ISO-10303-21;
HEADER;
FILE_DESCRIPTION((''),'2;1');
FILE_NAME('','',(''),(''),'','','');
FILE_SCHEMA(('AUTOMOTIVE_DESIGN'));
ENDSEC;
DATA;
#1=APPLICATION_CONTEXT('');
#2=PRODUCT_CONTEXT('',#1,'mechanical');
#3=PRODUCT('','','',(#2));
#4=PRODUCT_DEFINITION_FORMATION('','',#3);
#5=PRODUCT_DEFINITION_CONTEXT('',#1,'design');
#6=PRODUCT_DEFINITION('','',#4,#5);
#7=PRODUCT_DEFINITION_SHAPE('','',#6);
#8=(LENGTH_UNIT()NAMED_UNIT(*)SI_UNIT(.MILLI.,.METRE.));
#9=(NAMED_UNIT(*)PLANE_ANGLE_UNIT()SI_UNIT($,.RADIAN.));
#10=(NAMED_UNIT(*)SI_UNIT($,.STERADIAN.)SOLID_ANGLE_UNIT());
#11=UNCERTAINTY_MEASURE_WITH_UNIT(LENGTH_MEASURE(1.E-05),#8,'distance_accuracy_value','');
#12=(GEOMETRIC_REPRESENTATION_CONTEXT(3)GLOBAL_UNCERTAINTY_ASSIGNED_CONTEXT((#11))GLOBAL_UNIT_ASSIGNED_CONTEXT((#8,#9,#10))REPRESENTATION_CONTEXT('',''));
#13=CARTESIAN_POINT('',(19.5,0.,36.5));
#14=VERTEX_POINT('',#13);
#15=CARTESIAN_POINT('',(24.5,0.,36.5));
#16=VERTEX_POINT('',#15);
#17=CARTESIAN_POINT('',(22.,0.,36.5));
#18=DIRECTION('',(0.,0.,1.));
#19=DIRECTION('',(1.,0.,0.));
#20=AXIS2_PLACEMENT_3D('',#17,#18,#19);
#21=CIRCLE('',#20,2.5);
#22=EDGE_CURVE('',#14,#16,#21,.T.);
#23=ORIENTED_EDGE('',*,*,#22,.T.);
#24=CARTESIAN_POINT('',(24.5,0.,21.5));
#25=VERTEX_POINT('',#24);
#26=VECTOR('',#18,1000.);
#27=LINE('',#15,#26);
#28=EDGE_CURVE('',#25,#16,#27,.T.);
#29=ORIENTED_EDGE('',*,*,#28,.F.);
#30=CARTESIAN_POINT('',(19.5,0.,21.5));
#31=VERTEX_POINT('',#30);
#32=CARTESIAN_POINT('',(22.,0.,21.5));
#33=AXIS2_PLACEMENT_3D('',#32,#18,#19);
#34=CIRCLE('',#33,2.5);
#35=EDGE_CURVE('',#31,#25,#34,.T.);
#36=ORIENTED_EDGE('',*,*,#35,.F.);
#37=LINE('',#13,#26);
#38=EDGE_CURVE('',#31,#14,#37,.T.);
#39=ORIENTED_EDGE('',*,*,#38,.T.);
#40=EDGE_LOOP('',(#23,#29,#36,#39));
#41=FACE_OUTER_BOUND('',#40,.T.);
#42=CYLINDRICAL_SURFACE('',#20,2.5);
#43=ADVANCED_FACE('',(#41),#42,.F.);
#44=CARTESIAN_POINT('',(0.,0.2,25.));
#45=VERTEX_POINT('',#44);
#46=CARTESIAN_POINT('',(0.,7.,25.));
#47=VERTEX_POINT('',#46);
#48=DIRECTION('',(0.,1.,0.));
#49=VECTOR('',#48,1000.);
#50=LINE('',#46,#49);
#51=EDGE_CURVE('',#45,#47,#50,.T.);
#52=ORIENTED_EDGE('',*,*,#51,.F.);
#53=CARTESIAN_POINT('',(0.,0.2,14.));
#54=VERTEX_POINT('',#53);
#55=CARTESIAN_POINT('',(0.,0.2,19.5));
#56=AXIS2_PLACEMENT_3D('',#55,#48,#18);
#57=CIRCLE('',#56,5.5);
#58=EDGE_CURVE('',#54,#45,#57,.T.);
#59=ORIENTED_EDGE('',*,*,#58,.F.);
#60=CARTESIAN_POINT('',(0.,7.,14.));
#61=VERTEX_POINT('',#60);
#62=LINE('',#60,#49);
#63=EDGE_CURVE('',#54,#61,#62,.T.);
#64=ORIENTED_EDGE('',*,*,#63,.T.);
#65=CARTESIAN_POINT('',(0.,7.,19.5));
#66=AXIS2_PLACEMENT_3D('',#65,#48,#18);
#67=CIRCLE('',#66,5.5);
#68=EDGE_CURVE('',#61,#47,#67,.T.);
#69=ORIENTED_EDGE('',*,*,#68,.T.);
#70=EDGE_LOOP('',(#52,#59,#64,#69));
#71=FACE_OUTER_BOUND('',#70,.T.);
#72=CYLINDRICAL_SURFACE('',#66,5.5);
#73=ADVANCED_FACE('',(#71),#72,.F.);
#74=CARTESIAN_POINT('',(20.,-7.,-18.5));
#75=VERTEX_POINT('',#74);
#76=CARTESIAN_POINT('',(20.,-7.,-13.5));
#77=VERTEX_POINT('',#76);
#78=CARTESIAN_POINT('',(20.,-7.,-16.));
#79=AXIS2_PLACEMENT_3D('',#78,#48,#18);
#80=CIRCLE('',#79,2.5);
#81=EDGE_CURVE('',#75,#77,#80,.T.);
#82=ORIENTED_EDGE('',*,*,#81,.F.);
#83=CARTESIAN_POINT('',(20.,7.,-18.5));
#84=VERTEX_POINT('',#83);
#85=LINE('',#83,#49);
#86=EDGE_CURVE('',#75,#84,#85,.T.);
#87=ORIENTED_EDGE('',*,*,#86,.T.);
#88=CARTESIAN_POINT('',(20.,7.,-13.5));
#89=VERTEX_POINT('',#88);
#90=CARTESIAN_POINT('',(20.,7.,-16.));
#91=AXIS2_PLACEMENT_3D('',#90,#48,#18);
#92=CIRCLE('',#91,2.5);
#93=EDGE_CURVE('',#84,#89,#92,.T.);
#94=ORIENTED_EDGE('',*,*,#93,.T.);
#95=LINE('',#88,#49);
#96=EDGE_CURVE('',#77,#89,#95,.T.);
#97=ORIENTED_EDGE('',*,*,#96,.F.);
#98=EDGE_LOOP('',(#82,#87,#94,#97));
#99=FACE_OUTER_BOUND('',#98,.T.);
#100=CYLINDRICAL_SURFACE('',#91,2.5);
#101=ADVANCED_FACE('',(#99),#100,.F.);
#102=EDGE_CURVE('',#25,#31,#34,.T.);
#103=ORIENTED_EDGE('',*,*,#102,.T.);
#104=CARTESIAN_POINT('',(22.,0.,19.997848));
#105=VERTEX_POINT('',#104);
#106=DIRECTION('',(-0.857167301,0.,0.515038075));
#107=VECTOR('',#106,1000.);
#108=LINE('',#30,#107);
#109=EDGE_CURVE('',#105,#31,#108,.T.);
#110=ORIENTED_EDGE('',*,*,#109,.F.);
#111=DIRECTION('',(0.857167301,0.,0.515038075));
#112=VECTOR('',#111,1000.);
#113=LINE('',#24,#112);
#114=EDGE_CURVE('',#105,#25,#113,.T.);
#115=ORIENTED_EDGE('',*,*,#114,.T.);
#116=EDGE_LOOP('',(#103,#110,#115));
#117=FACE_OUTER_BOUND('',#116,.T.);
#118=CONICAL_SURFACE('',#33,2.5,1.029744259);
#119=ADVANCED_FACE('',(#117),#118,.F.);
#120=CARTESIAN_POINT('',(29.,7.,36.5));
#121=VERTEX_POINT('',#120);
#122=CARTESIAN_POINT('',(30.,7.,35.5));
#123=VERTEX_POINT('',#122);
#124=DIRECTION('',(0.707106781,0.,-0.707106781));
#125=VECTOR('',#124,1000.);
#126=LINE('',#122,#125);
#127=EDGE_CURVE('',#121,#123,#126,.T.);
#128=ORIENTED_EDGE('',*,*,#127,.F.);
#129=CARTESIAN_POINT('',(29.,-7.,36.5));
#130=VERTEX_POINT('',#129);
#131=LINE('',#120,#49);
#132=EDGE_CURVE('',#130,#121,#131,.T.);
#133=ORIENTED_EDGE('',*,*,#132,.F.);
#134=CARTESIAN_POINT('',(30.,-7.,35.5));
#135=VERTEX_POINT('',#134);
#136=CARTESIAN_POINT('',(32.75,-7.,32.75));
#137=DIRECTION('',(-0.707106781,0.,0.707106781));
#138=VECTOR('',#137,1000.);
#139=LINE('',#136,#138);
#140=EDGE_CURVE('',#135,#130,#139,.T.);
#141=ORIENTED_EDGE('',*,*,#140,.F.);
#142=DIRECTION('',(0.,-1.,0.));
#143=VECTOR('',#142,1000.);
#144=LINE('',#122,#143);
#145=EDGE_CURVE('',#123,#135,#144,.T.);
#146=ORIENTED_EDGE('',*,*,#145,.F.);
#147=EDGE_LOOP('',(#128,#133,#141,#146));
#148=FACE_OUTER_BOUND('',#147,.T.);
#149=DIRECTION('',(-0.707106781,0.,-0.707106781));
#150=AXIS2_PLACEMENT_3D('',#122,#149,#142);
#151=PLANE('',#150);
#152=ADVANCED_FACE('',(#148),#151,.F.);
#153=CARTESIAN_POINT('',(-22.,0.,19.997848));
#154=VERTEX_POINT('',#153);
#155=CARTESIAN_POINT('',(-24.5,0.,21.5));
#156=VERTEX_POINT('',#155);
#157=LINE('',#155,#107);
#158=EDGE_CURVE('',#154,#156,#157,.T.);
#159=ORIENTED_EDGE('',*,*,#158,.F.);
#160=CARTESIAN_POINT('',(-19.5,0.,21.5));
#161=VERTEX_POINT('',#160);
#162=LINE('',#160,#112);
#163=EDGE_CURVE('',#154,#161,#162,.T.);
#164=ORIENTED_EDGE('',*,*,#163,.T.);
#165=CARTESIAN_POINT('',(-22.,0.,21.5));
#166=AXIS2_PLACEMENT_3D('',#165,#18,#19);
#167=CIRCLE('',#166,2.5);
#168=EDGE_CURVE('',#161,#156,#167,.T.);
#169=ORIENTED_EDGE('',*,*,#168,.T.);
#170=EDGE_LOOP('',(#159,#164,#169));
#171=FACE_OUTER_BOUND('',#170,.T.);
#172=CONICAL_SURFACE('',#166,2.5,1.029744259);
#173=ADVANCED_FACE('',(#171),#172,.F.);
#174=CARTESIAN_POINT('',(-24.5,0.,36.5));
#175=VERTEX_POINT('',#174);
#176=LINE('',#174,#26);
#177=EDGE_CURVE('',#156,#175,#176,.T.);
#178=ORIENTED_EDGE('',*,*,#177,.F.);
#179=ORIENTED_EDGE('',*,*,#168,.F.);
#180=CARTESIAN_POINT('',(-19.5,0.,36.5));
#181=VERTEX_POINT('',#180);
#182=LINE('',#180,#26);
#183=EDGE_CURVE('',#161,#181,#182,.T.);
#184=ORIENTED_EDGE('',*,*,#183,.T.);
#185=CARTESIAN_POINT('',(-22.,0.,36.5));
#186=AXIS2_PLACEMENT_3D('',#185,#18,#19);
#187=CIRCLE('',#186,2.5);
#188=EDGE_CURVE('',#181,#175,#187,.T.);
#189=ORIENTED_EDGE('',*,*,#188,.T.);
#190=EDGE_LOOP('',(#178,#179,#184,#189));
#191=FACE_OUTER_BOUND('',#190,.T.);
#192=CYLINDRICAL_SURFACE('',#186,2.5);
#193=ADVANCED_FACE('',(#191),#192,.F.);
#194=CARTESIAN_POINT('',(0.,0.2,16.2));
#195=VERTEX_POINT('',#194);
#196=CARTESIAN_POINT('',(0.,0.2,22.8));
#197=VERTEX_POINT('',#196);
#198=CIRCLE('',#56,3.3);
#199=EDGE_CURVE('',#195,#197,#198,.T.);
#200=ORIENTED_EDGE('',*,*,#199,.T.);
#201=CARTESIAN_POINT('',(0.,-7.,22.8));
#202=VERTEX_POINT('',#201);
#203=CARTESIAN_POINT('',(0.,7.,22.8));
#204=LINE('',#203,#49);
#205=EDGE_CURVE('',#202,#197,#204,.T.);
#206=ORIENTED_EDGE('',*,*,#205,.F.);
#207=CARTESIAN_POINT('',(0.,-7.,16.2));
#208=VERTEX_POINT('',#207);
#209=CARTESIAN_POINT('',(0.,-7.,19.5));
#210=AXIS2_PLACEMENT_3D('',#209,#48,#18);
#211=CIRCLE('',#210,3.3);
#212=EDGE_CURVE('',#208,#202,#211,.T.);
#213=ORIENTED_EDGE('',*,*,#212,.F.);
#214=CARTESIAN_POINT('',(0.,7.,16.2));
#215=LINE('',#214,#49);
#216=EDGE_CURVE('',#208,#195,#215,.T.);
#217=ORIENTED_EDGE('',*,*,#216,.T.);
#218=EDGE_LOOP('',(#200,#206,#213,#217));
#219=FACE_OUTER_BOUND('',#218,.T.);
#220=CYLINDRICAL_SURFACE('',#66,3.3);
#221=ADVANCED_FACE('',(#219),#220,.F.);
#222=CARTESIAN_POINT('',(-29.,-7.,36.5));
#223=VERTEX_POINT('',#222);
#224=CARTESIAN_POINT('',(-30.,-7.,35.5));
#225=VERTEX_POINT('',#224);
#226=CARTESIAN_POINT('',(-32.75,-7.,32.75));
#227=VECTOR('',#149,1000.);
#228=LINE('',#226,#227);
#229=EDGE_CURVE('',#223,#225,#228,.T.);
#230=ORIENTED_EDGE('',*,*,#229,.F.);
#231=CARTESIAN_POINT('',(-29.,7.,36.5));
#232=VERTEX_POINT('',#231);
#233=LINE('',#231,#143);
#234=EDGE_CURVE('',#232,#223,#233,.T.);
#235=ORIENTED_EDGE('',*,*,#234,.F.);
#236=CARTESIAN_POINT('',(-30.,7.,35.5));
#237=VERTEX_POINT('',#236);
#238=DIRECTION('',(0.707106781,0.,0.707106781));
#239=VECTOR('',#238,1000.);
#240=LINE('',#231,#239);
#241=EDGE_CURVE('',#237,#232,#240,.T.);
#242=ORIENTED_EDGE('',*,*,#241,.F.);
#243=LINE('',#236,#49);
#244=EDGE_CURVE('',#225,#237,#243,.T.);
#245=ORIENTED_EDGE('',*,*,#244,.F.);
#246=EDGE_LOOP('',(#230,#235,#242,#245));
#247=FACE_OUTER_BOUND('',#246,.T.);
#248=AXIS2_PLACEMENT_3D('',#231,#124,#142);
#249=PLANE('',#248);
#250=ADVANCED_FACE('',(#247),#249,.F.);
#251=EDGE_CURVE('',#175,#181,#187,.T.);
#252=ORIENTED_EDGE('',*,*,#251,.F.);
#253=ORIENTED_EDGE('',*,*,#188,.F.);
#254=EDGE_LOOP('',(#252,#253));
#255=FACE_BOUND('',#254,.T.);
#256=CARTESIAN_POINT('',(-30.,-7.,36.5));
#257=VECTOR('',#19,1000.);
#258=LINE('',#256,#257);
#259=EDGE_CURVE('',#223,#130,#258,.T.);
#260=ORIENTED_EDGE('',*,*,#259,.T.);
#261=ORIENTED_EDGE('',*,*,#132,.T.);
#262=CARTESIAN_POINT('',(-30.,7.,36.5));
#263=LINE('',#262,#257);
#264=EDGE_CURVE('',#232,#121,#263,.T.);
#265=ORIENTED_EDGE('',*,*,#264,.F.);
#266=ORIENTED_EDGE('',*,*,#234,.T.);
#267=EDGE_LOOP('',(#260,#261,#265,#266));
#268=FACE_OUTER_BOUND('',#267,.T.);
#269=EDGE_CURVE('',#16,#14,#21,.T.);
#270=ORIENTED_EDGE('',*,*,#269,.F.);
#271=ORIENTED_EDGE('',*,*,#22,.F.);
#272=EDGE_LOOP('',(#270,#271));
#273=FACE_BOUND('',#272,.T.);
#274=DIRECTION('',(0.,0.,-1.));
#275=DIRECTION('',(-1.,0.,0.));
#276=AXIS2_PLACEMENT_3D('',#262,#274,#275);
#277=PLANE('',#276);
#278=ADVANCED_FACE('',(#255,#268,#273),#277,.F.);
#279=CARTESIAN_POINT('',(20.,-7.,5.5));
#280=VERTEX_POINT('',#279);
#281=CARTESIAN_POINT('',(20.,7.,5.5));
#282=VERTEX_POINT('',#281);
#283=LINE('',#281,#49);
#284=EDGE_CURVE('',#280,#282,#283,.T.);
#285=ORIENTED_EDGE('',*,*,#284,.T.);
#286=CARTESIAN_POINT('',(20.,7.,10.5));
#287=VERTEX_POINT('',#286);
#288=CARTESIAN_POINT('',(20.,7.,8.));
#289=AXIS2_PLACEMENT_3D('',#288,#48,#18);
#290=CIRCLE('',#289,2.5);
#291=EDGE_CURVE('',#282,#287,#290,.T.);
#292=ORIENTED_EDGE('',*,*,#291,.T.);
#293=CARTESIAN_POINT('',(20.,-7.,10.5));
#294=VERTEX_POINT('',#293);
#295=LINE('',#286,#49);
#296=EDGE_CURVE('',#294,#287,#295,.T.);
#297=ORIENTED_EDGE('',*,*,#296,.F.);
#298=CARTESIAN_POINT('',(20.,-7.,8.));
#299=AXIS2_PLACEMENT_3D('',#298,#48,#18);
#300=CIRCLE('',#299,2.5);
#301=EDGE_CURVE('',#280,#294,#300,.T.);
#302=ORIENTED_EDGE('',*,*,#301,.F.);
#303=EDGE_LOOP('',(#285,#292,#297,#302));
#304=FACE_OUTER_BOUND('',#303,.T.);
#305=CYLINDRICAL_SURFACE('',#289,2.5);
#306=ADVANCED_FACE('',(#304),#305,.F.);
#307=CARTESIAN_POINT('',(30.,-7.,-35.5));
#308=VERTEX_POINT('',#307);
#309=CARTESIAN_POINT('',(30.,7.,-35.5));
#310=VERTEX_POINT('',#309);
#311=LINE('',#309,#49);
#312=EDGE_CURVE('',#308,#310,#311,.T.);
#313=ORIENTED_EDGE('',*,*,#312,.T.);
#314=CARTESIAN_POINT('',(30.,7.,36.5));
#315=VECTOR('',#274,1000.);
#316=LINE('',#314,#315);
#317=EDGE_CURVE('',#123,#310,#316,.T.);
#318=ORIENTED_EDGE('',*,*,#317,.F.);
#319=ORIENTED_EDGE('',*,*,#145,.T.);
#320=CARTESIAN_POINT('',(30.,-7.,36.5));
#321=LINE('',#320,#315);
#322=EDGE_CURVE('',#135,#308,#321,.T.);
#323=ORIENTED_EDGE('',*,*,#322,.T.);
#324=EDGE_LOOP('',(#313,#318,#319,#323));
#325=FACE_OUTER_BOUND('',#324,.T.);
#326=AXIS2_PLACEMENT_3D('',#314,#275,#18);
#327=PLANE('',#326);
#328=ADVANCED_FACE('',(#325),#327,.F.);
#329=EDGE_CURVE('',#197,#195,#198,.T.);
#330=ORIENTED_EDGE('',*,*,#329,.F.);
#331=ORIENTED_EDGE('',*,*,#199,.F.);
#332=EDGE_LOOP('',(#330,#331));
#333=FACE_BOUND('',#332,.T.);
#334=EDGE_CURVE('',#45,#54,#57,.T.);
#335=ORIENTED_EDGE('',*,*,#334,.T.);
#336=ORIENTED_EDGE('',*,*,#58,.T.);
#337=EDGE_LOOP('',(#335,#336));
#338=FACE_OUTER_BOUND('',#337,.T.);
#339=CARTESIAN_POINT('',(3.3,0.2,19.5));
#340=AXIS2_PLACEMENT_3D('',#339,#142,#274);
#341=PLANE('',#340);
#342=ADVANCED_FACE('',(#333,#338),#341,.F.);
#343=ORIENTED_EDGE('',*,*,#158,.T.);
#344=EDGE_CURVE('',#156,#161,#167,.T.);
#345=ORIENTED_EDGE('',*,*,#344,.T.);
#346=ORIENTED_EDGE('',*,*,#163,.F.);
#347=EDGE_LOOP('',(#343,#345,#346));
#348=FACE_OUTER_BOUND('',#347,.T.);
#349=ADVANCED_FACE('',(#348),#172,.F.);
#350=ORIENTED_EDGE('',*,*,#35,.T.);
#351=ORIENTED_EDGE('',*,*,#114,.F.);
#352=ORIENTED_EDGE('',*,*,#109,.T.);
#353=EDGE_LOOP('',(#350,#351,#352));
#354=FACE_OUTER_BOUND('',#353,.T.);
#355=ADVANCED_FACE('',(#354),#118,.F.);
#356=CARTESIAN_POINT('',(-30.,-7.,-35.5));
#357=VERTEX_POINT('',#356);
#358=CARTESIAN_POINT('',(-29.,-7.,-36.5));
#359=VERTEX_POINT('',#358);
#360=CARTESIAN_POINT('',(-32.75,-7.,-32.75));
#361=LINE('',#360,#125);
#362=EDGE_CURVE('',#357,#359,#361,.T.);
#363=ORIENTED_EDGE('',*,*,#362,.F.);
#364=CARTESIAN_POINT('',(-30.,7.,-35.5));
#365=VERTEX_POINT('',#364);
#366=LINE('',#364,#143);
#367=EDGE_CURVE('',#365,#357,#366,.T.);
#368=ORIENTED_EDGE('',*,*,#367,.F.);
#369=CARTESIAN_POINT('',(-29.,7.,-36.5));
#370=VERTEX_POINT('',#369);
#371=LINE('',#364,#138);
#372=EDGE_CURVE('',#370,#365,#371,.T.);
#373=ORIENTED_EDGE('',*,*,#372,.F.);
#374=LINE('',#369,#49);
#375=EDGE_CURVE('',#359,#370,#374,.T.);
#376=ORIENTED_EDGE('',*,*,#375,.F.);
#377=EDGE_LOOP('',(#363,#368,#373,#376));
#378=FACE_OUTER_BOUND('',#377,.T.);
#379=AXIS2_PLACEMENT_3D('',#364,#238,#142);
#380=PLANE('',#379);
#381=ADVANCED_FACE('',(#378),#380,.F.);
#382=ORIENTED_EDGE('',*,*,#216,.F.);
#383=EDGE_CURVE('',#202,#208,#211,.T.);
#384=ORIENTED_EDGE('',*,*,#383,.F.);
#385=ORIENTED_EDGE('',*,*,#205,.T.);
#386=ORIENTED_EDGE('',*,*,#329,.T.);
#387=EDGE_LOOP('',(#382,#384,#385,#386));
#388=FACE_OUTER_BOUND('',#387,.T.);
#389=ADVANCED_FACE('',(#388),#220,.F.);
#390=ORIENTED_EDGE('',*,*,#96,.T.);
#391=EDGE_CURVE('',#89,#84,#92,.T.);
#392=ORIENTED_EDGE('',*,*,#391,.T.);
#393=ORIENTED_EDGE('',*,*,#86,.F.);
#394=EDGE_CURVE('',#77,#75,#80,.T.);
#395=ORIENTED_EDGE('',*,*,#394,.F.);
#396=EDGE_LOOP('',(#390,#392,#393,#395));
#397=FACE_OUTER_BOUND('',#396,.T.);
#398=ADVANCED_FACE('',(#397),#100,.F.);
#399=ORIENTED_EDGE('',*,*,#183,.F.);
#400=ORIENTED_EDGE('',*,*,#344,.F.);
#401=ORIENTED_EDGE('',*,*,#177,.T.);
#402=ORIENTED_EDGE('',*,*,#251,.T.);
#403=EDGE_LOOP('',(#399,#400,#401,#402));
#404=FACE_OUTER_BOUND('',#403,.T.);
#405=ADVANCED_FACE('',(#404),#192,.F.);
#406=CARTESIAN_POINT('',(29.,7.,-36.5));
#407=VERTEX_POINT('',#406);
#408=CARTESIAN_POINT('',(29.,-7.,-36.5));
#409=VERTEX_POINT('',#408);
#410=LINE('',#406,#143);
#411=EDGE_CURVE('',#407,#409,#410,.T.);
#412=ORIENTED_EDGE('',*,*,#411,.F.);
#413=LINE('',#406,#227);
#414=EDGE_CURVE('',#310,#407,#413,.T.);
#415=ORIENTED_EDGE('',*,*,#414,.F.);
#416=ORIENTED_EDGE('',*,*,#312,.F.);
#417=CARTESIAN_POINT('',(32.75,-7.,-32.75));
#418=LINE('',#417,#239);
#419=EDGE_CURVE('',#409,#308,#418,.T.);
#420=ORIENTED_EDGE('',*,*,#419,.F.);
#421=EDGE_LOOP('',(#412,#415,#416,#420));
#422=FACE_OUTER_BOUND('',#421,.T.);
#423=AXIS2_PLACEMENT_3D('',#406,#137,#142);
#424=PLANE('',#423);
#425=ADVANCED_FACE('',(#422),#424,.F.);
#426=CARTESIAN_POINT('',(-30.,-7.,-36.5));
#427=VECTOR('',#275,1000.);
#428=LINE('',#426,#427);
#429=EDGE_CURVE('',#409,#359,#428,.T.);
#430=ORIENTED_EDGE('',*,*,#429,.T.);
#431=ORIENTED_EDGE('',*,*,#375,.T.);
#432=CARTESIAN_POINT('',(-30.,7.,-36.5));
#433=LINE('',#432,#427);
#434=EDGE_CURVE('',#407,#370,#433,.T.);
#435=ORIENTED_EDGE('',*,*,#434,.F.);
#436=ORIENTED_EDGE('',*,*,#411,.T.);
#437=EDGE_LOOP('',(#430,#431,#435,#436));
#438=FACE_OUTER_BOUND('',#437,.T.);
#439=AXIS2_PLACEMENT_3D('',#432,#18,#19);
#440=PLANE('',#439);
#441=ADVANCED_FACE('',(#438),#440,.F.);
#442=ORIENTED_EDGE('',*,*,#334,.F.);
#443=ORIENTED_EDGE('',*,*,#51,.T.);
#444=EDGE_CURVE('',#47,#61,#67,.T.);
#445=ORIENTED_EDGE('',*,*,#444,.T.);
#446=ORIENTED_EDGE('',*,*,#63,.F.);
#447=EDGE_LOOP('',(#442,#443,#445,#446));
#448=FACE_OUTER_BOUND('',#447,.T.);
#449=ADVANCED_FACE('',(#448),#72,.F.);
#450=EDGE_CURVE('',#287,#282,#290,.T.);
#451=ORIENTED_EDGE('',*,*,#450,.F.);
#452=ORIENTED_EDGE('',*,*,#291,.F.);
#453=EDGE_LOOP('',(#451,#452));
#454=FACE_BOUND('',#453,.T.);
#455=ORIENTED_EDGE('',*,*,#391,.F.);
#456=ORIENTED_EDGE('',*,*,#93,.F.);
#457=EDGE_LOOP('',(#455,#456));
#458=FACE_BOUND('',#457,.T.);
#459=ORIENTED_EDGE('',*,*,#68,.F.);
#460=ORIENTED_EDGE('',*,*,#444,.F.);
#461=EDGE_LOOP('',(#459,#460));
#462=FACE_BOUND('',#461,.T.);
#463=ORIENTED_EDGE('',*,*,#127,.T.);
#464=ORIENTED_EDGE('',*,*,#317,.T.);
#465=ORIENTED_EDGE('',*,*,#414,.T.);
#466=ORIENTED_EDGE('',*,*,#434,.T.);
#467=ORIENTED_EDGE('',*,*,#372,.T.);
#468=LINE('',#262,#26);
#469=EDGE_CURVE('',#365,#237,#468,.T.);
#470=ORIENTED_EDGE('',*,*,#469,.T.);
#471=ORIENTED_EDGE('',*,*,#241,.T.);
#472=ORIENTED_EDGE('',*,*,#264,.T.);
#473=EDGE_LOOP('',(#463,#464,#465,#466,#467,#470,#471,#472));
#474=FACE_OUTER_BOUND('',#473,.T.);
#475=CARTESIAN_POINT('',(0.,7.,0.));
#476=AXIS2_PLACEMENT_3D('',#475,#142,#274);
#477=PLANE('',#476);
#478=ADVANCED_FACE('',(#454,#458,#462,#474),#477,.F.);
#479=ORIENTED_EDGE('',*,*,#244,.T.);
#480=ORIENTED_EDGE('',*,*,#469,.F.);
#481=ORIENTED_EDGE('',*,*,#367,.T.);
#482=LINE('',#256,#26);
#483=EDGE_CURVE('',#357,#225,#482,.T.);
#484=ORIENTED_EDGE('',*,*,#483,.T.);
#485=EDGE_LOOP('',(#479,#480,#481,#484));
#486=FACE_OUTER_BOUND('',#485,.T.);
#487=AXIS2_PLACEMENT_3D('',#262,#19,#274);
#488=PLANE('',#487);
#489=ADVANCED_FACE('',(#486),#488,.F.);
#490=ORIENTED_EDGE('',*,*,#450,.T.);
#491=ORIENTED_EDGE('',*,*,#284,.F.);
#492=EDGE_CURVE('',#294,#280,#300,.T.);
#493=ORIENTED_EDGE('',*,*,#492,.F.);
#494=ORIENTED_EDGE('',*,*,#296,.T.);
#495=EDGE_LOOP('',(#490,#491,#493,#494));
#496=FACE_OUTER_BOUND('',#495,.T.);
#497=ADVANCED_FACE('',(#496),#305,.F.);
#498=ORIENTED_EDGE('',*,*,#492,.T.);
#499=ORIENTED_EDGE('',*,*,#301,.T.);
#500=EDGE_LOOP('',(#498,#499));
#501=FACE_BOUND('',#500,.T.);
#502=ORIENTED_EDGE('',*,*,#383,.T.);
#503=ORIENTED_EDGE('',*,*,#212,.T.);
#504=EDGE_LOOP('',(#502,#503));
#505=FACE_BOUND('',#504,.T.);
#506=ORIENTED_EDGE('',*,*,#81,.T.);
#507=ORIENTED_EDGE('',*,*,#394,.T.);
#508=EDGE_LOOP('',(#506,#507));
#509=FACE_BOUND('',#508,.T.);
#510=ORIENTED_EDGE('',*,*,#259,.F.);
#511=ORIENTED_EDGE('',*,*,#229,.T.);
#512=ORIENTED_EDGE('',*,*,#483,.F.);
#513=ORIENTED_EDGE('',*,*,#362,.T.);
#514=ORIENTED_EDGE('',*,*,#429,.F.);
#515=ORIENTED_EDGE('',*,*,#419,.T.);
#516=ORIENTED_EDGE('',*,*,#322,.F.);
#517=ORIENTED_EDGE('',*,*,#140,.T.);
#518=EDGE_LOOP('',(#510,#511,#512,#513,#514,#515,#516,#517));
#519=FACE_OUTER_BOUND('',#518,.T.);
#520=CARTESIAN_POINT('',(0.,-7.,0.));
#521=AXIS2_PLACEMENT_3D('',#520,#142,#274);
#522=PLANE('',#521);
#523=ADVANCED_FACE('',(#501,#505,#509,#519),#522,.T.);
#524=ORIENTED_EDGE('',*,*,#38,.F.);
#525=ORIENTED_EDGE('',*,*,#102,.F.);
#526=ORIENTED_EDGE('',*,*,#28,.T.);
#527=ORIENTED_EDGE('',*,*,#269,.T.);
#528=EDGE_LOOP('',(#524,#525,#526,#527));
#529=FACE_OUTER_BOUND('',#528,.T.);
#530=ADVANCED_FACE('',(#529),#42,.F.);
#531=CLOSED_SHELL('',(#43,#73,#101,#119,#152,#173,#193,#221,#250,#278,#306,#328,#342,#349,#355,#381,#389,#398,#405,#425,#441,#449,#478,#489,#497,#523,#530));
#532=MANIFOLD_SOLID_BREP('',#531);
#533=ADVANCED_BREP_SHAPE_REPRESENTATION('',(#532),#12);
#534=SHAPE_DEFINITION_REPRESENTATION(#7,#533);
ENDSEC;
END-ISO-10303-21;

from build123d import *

# Parameters (mm, degrees)
SKETCH1_W                                            = 60
SKETCH1_H                                            = 73
BOSS_EXTRUDE1_DEPTH                                  = 7
M6_TAPPED_HOLE1_D                                    = 5
M6_TAPPED_HOLE1_DEPTH                                = 15
M6_TAPPED_HOLE1_TIP                                  = 1.502151548
M6_TAPPED_HOLE2_D                                    = 5
CHAMFER1_SIZE                                        = 1
HOLE_SIZE_PER_SOCKET_HEAD_CAP_SCREW_TYPE_D           = 6.6
HOLE_SIZE_PER_SOCKET_HEAD_CAP_SCREW_TYPE_CBORE_D     = 11
HOLE_SIZE_PER_SOCKET_HEAD_CAP_SCREW_TYPE_CBORE_DEPTH = 6.8


with BuildPart() as part:
    # Sketch1 → Boss-Extrude1 (new, symmetric)
    with BuildSketch(Plane(origin=(0, 0, 0), x_dir=(1, 0, 0), z_dir=(0, 1, 0))):
        Rectangle(SKETCH1_W, SKETCH1_H)
    extrude(amount=BOSS_EXTRUDE1_DEPTH, both=True)

    # M6 Tapped Hole1
    with Locations(Plane.XY.offset(36.5)):
        with Locations((22, 0), (-22, 0)):
            Hole(M6_TAPPED_HOLE1_D / 2, depth=M6_TAPPED_HOLE1_DEPTH)
            with Locations((0, 0, -(M6_TAPPED_HOLE1_DEPTH + M6_TAPPED_HOLE1_TIP / 2))):  # 118° drill point
                Cone(0, M6_TAPPED_HOLE1_D / 2, M6_TAPPED_HOLE1_TIP, mode=Mode.SUBTRACT)

    # M6 Tapped Hole2 (through all)
    with Locations(Plane(origin=(0, 7, 0), x_dir=(1, 0, 0), z_dir=(0, 1, 0))):
        with Locations((20, -8), (20, 16)):
            Hole(M6_TAPPED_HOLE2_D / 2)

    # Chamfer1
    chamfer1_edges = [part.edges().sort_by_distance(p)[0] for p in [
        (30, 0, 36.5),
        (-30, 0, 36.5),
        (-30, 0, -36.5),
        (30, 0, -36.5),
    ]]
    chamfer(chamfer1_edges, length=CHAMFER1_SIZE)

    # Hole Size per Socket Head Cap Screw Type1 (through all)
    with Locations(Plane(origin=(0, 7, 0), x_dir=(1, 0, 0), z_dir=(0, 1, 0))):
        with Locations((0, -19.5)):
            CounterBoreHole(HOLE_SIZE_PER_SOCKET_HEAD_CAP_SCREW_TYPE_D / 2, HOLE_SIZE_PER_SOCKET_HEAD_CAP_SCREW_TYPE_CBORE_D / 2, HOLE_SIZE_PER_SOCKET_HEAD_CAP_SCREW_TYPE_CBORE_DEPTH)


solid = part.part
